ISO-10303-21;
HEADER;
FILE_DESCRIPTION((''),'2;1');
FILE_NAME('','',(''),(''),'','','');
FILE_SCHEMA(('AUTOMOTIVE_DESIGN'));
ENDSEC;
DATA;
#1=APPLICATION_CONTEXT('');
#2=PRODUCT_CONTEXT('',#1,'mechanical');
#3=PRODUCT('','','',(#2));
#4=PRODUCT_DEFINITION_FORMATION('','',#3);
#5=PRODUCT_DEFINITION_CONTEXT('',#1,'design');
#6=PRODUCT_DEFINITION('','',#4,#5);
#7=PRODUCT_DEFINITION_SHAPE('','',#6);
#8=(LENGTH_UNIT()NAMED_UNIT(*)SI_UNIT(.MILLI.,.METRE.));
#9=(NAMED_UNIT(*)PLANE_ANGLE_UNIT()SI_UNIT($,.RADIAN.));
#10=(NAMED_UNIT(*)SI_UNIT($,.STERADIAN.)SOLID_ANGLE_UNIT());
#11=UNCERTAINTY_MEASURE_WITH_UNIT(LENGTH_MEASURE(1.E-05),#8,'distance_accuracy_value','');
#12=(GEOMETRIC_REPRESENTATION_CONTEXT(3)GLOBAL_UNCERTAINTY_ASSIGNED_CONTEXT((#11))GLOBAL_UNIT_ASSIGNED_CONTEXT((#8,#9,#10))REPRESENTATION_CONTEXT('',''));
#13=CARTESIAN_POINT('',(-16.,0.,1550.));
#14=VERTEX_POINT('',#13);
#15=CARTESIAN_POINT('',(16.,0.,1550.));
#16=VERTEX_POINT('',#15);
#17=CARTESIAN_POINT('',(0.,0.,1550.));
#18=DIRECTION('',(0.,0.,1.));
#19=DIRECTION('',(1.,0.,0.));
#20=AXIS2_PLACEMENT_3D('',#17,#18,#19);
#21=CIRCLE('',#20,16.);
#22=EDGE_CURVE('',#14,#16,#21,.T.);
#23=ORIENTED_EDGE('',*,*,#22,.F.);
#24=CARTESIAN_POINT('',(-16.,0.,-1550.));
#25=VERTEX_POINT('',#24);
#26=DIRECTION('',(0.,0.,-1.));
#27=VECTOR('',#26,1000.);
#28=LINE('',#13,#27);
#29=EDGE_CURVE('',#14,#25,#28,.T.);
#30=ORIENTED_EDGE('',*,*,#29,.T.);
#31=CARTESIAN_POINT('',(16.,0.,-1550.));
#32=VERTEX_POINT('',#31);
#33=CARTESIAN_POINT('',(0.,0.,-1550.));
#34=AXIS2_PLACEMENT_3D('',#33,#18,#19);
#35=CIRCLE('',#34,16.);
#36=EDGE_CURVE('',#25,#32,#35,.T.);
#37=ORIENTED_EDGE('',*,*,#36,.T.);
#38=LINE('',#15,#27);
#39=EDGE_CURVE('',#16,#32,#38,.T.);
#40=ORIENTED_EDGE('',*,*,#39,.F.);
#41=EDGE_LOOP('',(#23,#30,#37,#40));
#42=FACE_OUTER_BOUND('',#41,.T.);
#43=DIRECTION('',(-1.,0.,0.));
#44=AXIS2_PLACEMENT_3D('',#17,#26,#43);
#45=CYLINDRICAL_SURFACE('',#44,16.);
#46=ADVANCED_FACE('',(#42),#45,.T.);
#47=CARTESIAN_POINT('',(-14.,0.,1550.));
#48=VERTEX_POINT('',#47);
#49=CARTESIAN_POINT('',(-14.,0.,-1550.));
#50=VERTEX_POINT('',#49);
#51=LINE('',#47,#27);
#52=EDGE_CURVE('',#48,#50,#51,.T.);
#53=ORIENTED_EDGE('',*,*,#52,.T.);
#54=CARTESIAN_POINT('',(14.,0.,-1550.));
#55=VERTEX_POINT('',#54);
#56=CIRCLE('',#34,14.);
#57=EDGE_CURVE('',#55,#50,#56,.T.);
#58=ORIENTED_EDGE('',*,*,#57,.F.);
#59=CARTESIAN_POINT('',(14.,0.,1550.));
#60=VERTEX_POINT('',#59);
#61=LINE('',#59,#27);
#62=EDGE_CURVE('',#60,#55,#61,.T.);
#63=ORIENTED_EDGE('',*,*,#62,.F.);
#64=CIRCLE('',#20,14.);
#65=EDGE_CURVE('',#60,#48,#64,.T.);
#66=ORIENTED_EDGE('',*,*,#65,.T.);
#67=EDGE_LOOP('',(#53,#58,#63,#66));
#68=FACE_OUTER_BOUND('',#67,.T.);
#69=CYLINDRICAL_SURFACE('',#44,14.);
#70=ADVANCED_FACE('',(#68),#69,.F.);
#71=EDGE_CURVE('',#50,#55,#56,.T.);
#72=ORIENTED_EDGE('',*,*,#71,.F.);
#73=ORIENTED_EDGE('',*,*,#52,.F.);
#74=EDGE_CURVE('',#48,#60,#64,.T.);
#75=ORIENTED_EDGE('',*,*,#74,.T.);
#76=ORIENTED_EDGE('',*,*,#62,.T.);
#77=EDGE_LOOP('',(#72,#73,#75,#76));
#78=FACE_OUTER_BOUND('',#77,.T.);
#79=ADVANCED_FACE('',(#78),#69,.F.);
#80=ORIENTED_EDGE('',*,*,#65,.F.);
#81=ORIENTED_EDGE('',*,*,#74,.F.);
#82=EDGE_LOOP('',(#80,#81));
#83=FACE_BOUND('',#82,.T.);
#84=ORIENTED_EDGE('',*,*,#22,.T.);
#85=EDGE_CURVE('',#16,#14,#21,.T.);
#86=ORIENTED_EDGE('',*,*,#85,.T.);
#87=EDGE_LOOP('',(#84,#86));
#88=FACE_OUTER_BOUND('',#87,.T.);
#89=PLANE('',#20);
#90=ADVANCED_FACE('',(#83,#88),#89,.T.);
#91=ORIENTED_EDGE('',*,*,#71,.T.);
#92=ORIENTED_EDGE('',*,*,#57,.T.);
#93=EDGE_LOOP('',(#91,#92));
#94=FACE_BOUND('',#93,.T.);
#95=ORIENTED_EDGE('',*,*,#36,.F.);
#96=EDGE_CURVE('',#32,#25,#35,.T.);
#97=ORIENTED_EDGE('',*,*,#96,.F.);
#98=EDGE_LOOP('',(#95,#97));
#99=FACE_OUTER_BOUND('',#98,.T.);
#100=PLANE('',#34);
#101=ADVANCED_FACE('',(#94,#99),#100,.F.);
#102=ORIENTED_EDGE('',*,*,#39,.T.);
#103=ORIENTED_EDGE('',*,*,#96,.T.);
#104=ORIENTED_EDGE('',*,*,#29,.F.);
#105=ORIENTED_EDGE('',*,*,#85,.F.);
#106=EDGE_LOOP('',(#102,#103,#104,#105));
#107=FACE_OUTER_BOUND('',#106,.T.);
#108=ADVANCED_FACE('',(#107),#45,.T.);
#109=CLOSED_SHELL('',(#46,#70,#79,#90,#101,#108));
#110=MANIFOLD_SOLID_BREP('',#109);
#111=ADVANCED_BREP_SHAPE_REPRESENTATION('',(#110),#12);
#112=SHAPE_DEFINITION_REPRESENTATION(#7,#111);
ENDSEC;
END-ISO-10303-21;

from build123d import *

# Parameters (mm, degrees)
SKETCH_1_R      = 16
SKETCH_1_R_2    = 14
EXTRUDE_1_DEPTH = 1550


with BuildPart() as part:
    # 草图1 → 凸台-拉伸1 (new, symmetric)
    with BuildSketch(Plane.XY):
        Circle(SKETCH_1_R)
        Circle(SKETCH_1_R_2, mode=Mode.SUBTRACT)
    extrude(amount=EXTRUDE_1_DEPTH, both=True)


solid = part.part
